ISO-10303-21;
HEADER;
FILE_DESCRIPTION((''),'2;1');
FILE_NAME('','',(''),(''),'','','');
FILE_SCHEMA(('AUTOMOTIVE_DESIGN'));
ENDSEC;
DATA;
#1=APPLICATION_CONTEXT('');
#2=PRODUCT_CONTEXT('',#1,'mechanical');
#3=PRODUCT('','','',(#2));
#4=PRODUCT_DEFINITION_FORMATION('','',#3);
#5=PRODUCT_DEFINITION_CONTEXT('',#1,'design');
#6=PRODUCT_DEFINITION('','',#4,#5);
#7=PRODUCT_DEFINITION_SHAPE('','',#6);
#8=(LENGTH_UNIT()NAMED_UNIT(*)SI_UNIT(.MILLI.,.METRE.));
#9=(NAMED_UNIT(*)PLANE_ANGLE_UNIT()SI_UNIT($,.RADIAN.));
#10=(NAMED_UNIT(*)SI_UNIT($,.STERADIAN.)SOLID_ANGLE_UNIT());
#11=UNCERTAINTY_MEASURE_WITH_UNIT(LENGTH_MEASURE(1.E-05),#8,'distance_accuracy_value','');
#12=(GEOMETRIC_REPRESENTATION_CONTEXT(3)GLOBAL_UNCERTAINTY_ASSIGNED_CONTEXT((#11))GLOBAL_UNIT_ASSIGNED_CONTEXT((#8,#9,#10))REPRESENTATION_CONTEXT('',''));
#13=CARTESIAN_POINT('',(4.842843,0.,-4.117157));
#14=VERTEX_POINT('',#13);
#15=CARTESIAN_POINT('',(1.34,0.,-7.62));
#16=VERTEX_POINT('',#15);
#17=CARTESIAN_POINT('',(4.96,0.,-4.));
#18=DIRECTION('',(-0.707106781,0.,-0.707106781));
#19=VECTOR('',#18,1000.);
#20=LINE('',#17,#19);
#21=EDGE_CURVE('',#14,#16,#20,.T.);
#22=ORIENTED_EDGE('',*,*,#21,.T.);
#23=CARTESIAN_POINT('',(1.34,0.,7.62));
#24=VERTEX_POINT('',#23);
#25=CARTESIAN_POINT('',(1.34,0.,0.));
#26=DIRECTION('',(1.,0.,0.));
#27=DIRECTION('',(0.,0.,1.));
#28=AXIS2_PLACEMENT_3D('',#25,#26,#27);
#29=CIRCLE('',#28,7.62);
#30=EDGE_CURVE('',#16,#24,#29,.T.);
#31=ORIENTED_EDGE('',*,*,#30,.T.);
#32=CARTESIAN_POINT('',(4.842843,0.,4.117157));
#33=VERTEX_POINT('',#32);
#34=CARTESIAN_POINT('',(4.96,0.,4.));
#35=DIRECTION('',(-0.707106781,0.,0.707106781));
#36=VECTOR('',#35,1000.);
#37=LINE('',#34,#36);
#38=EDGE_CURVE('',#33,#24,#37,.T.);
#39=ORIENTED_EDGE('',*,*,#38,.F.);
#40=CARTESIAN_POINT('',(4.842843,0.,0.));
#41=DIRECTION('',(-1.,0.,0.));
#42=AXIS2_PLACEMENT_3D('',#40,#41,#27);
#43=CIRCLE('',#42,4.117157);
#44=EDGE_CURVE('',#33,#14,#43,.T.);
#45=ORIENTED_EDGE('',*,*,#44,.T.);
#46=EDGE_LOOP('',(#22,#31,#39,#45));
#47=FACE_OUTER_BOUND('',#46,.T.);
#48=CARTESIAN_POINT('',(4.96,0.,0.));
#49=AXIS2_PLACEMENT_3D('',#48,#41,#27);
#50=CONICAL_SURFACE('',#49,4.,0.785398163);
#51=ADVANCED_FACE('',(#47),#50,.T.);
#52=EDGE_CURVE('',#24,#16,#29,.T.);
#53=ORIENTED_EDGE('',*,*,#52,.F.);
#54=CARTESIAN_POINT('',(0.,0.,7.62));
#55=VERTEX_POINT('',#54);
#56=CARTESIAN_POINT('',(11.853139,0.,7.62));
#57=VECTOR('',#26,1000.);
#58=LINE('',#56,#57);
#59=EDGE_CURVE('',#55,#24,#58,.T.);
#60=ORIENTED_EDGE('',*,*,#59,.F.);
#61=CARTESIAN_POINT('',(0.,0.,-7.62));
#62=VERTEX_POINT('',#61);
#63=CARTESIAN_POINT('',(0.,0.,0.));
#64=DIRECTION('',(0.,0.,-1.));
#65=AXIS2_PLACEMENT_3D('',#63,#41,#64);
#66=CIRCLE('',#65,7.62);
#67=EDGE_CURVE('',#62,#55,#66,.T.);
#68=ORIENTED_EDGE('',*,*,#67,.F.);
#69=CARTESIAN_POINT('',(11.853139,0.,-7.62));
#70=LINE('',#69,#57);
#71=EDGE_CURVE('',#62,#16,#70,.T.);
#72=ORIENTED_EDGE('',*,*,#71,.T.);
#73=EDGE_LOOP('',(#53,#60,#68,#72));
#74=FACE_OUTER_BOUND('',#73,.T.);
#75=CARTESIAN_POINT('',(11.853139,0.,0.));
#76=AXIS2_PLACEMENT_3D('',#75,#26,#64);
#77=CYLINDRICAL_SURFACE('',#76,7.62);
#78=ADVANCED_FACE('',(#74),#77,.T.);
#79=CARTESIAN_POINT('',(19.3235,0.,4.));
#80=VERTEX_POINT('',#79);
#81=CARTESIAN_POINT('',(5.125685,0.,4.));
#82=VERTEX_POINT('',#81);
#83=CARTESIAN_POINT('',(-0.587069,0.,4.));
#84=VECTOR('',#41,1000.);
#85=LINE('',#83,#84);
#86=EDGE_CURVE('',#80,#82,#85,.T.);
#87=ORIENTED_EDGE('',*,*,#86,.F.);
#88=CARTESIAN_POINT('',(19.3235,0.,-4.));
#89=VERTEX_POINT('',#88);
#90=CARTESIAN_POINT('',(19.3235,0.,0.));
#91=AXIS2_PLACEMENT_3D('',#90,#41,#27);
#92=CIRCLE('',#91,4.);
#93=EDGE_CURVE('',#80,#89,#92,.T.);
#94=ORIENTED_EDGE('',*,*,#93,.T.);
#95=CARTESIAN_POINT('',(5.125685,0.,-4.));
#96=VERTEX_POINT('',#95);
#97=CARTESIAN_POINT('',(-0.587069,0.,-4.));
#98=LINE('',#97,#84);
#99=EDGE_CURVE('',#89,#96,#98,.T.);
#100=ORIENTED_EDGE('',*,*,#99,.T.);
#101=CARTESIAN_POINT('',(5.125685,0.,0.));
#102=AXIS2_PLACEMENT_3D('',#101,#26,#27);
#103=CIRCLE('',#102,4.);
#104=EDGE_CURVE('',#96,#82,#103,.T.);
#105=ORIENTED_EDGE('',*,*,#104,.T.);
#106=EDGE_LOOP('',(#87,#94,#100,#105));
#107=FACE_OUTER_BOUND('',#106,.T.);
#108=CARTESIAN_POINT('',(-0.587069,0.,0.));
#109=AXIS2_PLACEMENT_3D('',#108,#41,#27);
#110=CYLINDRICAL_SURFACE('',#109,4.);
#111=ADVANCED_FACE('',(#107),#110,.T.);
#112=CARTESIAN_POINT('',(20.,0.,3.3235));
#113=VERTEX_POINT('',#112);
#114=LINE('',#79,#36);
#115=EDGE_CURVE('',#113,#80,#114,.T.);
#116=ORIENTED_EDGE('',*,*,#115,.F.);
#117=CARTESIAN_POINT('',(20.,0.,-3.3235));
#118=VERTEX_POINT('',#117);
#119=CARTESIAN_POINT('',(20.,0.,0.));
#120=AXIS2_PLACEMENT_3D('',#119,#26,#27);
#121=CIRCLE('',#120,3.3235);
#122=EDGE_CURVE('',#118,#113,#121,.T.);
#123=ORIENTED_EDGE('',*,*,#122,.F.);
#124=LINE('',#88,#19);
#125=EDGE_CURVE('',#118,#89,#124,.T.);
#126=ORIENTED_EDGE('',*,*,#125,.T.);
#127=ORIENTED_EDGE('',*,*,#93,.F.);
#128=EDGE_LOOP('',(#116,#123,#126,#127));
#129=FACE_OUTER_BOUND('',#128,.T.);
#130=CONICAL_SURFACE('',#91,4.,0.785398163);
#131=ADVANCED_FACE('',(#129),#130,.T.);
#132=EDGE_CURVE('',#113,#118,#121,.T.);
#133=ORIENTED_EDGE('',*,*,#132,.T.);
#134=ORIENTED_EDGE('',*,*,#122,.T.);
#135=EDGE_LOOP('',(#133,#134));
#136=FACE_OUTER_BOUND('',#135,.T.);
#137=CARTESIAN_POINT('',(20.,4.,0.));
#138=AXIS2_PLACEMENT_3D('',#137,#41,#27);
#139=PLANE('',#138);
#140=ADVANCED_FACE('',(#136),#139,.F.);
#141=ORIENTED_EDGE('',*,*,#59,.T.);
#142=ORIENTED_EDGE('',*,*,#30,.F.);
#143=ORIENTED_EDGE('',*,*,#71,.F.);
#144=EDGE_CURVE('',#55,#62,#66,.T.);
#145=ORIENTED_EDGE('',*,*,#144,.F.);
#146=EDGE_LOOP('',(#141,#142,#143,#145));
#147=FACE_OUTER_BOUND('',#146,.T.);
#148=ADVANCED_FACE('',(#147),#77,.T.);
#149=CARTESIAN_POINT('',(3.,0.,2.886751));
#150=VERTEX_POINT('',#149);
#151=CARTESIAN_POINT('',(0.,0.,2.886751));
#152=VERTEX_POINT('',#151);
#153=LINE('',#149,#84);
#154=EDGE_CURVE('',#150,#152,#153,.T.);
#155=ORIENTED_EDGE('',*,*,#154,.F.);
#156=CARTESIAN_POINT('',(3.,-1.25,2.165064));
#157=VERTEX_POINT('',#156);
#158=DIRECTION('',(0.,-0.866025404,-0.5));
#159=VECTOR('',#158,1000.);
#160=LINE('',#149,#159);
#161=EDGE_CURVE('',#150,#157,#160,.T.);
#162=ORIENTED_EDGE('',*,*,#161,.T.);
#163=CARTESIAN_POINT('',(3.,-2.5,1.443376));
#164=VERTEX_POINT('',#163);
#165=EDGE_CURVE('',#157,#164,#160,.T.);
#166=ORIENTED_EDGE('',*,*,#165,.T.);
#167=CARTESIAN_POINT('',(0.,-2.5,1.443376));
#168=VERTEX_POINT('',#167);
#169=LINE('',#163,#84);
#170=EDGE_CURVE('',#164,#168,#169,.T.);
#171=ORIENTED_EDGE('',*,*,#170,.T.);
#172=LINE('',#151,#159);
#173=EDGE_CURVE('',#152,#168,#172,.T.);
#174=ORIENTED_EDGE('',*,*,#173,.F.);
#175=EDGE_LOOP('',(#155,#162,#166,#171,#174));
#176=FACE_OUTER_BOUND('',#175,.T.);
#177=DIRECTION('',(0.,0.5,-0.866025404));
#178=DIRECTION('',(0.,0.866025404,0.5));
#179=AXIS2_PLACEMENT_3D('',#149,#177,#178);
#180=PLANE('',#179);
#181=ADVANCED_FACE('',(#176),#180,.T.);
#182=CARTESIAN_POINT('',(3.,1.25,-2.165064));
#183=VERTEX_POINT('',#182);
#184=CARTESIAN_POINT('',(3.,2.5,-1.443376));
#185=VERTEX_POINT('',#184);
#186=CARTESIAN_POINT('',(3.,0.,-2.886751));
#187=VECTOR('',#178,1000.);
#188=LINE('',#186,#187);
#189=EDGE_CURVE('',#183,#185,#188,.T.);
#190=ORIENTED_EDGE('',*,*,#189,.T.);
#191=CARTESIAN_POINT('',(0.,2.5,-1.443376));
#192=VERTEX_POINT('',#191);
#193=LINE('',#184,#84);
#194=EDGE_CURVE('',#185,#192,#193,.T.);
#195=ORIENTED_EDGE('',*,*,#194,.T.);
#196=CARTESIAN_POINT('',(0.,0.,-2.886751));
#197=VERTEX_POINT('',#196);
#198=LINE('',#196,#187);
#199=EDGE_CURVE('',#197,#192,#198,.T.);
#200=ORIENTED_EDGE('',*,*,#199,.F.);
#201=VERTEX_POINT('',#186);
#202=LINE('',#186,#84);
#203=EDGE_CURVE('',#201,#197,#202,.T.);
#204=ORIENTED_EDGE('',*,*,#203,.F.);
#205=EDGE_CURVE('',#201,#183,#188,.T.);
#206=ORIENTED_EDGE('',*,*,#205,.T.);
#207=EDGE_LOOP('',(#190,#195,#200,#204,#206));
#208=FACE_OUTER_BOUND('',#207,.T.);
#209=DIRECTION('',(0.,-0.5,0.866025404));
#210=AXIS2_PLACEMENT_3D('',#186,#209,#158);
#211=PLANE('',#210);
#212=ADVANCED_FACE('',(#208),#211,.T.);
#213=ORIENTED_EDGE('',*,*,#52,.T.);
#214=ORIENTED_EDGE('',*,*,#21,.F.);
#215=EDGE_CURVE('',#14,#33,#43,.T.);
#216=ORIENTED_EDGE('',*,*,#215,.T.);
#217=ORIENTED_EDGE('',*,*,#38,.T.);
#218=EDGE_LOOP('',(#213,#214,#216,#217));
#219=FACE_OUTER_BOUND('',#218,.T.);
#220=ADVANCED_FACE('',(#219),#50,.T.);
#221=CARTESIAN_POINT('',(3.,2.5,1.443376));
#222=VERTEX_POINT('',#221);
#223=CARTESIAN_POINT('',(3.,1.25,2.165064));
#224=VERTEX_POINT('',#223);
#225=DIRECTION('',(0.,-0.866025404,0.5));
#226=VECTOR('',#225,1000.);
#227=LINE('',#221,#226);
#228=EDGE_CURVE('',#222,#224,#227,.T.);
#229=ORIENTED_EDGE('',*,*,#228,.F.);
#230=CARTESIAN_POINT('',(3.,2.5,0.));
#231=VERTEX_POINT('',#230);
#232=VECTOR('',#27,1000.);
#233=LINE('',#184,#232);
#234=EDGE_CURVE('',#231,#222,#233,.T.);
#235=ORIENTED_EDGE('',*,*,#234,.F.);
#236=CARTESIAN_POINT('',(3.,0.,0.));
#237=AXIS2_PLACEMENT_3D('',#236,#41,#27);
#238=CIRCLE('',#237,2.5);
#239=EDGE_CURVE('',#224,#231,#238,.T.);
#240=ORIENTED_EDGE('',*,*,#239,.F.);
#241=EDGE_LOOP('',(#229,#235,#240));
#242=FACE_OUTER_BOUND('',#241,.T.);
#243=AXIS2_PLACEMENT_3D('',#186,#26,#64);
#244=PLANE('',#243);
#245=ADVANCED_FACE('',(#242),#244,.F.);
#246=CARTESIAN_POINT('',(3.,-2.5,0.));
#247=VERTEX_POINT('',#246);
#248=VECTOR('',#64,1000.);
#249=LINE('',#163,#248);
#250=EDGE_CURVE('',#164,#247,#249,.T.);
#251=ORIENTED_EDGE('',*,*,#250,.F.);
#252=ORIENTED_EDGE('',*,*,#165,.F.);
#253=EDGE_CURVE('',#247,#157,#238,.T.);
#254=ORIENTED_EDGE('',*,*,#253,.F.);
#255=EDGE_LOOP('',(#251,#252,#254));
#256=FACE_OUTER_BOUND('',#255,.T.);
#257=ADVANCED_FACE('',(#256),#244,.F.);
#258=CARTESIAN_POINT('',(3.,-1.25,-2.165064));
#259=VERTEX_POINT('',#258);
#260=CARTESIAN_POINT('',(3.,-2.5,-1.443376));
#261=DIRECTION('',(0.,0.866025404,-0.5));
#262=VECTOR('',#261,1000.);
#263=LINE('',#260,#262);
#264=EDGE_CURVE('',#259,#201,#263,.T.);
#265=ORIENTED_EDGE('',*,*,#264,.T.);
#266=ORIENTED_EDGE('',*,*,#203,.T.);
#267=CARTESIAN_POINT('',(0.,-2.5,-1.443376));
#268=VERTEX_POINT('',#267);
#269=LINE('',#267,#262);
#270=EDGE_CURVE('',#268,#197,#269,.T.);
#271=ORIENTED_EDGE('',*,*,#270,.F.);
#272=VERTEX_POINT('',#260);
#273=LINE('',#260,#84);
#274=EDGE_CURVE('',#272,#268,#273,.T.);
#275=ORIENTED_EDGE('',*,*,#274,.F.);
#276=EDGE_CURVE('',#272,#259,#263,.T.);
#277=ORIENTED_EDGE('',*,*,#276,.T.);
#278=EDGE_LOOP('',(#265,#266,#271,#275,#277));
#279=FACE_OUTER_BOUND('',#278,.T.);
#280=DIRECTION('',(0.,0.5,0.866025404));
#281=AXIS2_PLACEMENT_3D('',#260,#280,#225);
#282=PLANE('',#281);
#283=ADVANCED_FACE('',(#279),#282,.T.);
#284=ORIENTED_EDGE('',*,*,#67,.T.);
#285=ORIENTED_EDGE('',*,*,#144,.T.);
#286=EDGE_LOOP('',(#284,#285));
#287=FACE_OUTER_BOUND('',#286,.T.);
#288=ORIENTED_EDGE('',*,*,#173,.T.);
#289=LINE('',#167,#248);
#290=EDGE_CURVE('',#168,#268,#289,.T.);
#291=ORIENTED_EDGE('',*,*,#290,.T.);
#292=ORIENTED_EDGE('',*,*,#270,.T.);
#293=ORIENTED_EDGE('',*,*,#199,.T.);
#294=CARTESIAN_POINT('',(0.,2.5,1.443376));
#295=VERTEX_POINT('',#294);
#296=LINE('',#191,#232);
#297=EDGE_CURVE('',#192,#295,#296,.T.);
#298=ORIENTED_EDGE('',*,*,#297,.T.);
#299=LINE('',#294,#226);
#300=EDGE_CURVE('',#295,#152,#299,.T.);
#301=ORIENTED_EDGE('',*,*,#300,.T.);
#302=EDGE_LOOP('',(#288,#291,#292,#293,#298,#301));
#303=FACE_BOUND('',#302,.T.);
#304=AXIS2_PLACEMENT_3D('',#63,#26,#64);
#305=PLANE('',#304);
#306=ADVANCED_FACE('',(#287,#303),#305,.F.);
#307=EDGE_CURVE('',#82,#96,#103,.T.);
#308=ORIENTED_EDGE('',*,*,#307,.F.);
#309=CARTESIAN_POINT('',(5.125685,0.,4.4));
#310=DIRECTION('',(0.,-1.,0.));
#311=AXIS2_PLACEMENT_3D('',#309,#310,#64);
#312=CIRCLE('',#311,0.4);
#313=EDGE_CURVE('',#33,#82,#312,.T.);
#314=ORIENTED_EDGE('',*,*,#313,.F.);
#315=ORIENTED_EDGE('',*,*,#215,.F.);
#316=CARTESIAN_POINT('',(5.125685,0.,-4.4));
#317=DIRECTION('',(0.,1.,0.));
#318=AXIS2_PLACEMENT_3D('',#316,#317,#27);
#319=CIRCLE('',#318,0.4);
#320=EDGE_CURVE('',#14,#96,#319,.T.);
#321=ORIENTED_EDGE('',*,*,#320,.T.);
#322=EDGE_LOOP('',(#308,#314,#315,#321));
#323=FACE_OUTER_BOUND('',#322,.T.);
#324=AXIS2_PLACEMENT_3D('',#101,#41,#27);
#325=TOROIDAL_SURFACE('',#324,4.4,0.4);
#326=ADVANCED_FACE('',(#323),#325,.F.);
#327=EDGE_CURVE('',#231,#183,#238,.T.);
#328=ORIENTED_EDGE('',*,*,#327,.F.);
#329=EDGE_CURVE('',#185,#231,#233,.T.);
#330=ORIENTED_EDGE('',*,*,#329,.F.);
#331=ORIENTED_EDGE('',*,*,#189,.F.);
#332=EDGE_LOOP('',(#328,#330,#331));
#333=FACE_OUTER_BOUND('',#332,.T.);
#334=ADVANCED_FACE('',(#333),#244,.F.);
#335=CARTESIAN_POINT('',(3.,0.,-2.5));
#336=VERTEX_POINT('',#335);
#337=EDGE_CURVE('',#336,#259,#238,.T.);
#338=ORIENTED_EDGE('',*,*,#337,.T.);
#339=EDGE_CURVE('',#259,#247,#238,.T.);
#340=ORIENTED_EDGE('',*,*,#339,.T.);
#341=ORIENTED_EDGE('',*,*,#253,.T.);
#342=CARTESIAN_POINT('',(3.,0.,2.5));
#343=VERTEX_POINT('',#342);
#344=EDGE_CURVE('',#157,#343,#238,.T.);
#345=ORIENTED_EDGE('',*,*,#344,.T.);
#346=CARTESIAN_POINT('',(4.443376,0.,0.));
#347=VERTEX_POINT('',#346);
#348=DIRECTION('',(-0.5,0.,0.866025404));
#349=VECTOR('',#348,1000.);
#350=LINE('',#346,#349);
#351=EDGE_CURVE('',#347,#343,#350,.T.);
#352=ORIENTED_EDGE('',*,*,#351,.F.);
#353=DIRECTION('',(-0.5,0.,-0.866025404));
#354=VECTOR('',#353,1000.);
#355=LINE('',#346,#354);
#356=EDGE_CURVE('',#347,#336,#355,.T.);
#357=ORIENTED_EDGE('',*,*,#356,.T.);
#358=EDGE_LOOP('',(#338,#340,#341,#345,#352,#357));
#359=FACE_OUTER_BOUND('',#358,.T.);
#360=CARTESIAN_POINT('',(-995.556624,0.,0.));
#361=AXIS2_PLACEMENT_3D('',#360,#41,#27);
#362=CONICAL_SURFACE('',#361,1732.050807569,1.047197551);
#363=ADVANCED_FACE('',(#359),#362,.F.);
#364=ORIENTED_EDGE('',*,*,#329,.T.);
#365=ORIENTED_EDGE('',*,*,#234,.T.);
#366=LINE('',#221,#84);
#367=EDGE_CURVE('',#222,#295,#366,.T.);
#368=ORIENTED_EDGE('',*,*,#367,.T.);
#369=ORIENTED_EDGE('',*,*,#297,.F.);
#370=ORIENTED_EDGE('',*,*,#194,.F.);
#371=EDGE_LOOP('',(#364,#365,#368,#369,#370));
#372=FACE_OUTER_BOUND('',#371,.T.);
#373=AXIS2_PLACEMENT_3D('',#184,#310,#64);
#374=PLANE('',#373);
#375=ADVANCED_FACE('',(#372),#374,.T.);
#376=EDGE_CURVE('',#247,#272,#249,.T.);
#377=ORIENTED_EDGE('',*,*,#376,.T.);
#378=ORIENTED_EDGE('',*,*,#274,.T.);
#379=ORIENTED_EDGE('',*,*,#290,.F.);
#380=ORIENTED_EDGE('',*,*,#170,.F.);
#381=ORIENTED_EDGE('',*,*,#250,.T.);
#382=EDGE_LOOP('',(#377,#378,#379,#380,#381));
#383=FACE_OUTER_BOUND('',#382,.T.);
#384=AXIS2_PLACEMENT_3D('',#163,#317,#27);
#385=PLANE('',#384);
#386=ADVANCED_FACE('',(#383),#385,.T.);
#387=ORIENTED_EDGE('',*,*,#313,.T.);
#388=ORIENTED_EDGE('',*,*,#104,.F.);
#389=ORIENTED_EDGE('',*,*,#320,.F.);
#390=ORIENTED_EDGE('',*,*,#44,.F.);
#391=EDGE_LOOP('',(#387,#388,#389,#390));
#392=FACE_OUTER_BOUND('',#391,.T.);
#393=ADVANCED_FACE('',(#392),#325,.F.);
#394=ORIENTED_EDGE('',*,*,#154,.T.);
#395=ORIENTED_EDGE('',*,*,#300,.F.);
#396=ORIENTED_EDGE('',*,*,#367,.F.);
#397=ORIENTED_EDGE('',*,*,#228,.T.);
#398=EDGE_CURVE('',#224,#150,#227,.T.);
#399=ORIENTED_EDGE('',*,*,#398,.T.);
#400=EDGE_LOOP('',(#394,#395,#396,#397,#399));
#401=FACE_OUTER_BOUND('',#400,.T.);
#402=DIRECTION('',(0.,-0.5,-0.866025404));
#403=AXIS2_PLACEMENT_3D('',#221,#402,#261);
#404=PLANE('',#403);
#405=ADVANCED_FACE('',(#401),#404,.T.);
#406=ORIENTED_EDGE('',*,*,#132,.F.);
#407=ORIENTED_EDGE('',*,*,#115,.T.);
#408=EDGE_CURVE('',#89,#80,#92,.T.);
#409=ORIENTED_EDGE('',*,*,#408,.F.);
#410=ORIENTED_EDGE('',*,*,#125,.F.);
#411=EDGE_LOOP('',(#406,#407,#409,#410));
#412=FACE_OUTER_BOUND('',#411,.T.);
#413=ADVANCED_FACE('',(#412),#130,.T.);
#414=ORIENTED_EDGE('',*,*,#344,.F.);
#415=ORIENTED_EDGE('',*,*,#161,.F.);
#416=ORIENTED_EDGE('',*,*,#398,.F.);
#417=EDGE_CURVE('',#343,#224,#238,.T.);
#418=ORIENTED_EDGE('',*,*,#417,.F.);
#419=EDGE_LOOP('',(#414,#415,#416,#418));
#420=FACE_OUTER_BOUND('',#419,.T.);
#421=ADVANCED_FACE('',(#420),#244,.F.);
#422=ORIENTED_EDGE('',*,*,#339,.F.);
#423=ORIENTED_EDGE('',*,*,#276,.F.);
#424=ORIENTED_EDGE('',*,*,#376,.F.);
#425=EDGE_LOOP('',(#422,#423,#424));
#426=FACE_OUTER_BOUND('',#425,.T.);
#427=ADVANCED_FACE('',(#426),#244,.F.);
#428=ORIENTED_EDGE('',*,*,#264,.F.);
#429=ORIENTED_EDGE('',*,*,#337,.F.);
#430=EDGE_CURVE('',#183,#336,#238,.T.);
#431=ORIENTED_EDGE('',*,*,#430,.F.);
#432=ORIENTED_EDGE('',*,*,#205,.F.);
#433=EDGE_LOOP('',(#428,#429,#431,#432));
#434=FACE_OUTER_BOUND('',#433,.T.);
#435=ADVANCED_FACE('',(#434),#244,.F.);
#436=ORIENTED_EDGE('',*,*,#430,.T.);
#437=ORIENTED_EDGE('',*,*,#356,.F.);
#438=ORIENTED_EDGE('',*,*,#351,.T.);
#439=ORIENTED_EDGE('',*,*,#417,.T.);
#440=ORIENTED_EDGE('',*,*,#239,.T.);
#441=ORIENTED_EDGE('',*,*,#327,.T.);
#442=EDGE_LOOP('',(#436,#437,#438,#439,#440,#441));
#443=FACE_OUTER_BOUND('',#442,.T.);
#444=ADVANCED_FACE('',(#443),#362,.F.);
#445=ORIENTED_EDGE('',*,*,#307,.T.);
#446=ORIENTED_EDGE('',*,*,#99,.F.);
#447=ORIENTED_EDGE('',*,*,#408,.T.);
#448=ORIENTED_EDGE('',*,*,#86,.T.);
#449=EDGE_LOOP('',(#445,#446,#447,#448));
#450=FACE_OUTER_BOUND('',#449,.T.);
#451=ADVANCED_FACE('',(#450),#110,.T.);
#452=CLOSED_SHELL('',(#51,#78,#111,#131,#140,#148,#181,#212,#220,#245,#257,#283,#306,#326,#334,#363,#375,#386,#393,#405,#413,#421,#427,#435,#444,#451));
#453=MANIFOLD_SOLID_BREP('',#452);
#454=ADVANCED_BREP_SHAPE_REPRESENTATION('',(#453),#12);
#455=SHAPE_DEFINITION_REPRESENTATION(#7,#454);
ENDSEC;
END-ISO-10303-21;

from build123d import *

# Parameters (mm, degrees)
HEXAGONSOCKET_DEPTH = 3
HEADFILLET_R        = 0.4
CHAMFER_2_SIZE      = 0.6765
SKETCH4_W           = 5
SKETCH4_H           = 5


with BuildPart() as part:
    # Sketch1 → Base (revolve)
    with BuildSketch(Plane.XY, mode=Mode.PRIVATE) as base_sk:
        Polygon((0, 0), (0, 8.96), (4.96, 4), (20, 4), (20, 0), align=None)
    revolve(base_sk.sketch.rotate(Axis((-0.587069181, 0, 0), (1, 0, 0)), 90), axis=Axis((-0.587069181, 0, 0), (1, 0, 0)))

    # Sketch2 → HexagonSocket (cut)
    with BuildSketch(Plane(origin=(0, 0, 0), x_dir=(0, 0, -1), z_dir=(1, 0, 0))):
        Polygon((2.886751346, 0), (1.443375673, 2.5), (-1.443375673, 2.5), (-2.886751346, 0), (-1.443375673, -2.5), (1.443375673, -2.5), align=None)
    extrude(amount=HEXAGONSOCKET_DEPTH, mode=Mode.SUBTRACT)

    # Sketch3 → Cut-Revolve1 (revolve, cut)
    with BuildSketch(Plane.XY, mode=Mode.PRIVATE) as cut_revolve1_sk:
        Polygon((3, 2.5), (4.443375673, 0), (3, 0), align=None)
    revolve(cut_revolve1_sk.sketch.rotate(Axis((-0.439109555, 0, 0), (1, 0, 0)), 90), axis=Axis((-0.439109555, 0, 0), (1, 0, 0)), mode=Mode.SUBTRACT)

    # HeadFillet
    headfillet_edges = [part.edges().sort_by_distance(p)[0] for p in [
        (4.96, 0, -4),
    ]]
    fillet(headfillet_edges, radius=HEADFILLET_R)

    # Chamfer 2
    chamfer_2_edges = [part.edges().sort_by_distance(p)[0] for p in [
        (20, 0, -4),
    ]]
    chamfer(chamfer_2_edges, length=CHAMFER_2_SIZE)

    # Sketch4 → Cut-Revolve2 (revolve, cut)
    with BuildSketch(Plane(origin=(0, 0, 0), x_dir=(1, 0, 0), z_dir=(0, 1, 0)), mode=Mode.PRIVATE) as cut_revolve2_sk:
        with Locations((0.5, 10.12)):
            Rectangle(SKETCH4_W, SKETCH4_H)
    revolve(cut_revolve2_sk.sketch.rotate(Axis((11.853138686, 0, 0), (-1, 0, 0)), 180), axis=Axis((11.853138686, 0, 0), (-1, 0, 0)), mode=Mode.SUBTRACT)


solid = part.part
